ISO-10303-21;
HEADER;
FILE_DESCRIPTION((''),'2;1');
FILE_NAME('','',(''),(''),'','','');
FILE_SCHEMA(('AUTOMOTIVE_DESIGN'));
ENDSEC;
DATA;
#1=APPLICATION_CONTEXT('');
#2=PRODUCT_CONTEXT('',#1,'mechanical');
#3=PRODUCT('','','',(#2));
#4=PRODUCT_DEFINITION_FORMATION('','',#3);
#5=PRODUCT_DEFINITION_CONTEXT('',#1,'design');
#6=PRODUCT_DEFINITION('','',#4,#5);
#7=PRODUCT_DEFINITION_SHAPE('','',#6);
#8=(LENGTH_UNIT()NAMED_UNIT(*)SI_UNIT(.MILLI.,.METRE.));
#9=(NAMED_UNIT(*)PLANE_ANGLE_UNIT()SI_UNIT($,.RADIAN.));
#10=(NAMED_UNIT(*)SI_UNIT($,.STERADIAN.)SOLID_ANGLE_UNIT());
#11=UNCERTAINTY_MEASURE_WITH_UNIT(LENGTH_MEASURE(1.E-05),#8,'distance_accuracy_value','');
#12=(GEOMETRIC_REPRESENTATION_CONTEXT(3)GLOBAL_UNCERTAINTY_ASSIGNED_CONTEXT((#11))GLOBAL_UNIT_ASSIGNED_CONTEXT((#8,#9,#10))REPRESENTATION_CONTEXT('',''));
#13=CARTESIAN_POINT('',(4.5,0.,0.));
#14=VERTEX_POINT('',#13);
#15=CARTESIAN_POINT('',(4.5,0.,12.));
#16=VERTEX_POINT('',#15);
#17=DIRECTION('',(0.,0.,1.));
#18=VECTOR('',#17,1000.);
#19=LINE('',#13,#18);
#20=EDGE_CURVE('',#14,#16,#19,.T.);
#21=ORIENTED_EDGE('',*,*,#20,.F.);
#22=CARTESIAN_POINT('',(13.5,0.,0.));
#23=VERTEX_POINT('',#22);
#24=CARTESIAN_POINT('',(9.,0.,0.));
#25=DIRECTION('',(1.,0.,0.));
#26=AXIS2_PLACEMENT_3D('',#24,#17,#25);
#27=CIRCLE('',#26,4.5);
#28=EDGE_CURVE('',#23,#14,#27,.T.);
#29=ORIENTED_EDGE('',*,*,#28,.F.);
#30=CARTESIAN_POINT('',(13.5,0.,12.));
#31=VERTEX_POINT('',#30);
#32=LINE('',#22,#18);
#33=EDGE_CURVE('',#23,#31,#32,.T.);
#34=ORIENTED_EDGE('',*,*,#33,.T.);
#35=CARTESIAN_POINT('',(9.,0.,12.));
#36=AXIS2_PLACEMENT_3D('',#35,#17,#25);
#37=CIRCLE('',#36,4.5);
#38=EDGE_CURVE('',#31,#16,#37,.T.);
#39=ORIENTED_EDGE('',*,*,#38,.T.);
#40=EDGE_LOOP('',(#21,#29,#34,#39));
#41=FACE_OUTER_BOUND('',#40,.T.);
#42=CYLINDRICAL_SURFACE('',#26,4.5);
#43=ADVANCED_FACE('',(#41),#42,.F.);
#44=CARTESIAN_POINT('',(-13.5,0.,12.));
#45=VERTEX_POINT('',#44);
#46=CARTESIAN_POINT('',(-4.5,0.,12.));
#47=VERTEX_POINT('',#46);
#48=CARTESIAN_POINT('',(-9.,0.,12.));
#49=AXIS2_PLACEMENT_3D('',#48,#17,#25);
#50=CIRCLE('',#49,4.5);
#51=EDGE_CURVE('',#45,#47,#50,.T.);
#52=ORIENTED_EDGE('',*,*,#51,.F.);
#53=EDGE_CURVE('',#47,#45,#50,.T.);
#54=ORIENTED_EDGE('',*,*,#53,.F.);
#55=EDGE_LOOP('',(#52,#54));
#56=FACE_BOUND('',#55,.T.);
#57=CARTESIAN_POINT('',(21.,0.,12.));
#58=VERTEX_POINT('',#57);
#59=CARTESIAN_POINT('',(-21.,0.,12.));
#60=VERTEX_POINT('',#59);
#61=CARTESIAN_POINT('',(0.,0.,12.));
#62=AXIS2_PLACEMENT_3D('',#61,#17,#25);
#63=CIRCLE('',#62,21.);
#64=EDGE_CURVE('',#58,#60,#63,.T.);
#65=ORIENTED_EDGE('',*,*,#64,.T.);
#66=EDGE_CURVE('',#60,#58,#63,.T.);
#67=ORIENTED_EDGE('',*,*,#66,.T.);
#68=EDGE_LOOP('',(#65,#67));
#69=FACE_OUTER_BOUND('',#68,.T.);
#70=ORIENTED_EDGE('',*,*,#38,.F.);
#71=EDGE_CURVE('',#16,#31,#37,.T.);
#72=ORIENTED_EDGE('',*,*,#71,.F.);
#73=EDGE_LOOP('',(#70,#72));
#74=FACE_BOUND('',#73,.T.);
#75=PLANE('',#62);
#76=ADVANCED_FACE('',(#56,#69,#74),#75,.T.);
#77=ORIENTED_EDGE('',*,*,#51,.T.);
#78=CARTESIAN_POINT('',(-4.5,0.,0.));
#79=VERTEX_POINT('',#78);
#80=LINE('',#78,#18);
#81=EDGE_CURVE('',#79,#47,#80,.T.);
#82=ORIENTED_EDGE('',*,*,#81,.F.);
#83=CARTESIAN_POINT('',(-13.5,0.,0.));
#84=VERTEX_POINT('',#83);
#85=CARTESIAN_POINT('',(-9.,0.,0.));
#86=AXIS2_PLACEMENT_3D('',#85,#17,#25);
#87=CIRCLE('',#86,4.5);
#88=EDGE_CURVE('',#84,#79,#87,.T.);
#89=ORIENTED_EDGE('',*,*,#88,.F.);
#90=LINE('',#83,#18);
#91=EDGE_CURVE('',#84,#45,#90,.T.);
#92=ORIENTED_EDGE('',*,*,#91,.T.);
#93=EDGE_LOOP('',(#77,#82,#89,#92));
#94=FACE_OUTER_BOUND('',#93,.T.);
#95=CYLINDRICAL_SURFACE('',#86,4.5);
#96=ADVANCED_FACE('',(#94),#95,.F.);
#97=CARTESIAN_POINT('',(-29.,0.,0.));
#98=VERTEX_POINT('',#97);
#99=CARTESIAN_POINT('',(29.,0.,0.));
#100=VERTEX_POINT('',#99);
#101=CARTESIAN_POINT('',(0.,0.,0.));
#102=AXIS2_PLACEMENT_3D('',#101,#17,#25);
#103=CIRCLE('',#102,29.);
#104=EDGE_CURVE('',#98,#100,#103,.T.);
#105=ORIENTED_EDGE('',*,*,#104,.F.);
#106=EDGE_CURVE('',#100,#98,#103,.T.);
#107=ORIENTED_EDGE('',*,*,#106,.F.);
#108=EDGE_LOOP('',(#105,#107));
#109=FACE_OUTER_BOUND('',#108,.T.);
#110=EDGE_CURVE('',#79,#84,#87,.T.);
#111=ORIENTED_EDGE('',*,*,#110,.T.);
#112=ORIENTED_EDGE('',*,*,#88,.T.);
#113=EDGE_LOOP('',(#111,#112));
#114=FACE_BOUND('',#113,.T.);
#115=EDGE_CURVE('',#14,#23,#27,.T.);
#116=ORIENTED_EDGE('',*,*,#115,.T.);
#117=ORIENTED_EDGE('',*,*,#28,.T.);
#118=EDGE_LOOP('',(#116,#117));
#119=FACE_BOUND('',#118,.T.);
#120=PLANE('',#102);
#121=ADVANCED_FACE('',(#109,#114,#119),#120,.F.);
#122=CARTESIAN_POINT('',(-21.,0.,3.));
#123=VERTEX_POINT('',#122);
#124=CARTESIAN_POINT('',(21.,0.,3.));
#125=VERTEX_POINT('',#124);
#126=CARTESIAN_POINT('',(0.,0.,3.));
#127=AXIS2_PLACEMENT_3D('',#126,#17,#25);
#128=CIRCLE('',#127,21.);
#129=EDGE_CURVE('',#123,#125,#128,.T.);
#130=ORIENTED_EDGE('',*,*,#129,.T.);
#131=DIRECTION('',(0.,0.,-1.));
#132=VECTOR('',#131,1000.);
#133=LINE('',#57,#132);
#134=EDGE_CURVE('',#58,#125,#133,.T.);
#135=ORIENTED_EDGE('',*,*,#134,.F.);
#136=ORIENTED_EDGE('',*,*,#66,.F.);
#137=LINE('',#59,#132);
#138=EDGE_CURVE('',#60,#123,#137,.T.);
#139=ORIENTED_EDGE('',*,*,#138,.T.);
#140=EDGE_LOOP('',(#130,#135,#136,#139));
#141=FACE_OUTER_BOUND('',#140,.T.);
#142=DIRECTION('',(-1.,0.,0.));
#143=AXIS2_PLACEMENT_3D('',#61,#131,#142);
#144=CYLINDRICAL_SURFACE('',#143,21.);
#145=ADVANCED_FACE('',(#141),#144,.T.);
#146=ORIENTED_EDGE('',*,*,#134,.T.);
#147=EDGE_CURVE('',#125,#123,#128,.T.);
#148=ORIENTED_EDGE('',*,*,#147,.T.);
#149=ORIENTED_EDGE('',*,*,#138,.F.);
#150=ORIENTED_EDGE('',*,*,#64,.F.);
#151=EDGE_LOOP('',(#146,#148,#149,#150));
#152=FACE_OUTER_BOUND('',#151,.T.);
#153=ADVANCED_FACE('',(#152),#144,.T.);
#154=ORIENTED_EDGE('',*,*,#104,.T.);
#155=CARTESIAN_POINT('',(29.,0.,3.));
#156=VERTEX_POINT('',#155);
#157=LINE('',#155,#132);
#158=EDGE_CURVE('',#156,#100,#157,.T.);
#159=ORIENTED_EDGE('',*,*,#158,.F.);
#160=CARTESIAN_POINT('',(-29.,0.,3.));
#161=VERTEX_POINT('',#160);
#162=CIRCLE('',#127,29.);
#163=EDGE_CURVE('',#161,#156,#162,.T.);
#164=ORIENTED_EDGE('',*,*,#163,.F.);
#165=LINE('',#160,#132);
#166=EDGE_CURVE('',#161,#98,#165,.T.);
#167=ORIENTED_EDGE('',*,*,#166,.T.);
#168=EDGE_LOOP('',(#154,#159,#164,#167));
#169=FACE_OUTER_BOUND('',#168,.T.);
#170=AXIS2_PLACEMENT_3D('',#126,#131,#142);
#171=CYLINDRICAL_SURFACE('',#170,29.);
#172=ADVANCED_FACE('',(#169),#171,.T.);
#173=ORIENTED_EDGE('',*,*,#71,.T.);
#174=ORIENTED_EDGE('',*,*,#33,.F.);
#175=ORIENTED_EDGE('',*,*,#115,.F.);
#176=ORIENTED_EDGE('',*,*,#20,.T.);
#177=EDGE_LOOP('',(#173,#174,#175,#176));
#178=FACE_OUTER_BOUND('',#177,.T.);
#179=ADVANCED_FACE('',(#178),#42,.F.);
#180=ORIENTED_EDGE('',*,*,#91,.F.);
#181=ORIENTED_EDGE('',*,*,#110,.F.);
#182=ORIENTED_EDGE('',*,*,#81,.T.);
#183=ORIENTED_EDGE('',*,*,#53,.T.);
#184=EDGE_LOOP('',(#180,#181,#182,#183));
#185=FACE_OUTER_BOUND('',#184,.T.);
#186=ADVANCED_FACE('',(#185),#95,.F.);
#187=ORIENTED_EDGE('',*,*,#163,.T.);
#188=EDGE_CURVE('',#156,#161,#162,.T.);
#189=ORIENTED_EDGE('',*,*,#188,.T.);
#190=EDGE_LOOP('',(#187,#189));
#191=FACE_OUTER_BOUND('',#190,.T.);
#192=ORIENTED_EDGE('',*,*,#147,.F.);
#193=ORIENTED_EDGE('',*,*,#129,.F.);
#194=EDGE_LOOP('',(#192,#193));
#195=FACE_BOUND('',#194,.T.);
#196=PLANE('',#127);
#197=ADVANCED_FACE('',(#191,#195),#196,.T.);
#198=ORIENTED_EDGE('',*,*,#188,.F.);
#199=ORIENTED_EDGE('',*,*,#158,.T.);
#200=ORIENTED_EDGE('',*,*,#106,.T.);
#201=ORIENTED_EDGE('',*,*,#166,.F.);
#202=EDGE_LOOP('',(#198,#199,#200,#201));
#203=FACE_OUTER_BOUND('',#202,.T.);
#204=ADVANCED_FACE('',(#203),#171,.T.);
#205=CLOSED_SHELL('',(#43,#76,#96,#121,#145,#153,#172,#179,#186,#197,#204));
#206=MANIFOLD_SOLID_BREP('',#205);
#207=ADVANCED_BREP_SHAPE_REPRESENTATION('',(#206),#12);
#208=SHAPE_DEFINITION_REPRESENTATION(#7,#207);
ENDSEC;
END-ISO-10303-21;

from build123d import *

# Parameters (mm, degrees)
SKETCH_1_R          = 29
EXTRUDE_1_DEPTH     = 3
SKETCH_2_R          = 21
EXTRUDE_2_DEPTH     = 9
SKETCH_3_R          = 4.5
CUT_EXTRUDE_1_DEPTH = 43.731721238


with BuildPart() as part:
    # 草图1 → 凸台-拉伸1 (new body)
    with BuildSketch(Plane.XY):
        Circle(SKETCH_1_R)
    extrude(amount=EXTRUDE_1_DEPTH)

    # 草图2 → 凸台-拉伸2 (add)
    with BuildSketch(Plane.XY.offset(3)):
        Circle(SKETCH_2_R)
    extrude(amount=EXTRUDE_2_DEPTH)

    # 草图3 → 切除-拉伸1 (cut, through all)
    with BuildSketch(Plane.XY.offset(12)):
        with Locations((-9, 0)):
            Circle(SKETCH_3_R)
        with Locations((9, 0)):
            Circle(SKETCH_3_R)
    extrude(amount=-CUT_EXTRUDE_1_DEPTH, mode=Mode.SUBTRACT)


solid = part.part
